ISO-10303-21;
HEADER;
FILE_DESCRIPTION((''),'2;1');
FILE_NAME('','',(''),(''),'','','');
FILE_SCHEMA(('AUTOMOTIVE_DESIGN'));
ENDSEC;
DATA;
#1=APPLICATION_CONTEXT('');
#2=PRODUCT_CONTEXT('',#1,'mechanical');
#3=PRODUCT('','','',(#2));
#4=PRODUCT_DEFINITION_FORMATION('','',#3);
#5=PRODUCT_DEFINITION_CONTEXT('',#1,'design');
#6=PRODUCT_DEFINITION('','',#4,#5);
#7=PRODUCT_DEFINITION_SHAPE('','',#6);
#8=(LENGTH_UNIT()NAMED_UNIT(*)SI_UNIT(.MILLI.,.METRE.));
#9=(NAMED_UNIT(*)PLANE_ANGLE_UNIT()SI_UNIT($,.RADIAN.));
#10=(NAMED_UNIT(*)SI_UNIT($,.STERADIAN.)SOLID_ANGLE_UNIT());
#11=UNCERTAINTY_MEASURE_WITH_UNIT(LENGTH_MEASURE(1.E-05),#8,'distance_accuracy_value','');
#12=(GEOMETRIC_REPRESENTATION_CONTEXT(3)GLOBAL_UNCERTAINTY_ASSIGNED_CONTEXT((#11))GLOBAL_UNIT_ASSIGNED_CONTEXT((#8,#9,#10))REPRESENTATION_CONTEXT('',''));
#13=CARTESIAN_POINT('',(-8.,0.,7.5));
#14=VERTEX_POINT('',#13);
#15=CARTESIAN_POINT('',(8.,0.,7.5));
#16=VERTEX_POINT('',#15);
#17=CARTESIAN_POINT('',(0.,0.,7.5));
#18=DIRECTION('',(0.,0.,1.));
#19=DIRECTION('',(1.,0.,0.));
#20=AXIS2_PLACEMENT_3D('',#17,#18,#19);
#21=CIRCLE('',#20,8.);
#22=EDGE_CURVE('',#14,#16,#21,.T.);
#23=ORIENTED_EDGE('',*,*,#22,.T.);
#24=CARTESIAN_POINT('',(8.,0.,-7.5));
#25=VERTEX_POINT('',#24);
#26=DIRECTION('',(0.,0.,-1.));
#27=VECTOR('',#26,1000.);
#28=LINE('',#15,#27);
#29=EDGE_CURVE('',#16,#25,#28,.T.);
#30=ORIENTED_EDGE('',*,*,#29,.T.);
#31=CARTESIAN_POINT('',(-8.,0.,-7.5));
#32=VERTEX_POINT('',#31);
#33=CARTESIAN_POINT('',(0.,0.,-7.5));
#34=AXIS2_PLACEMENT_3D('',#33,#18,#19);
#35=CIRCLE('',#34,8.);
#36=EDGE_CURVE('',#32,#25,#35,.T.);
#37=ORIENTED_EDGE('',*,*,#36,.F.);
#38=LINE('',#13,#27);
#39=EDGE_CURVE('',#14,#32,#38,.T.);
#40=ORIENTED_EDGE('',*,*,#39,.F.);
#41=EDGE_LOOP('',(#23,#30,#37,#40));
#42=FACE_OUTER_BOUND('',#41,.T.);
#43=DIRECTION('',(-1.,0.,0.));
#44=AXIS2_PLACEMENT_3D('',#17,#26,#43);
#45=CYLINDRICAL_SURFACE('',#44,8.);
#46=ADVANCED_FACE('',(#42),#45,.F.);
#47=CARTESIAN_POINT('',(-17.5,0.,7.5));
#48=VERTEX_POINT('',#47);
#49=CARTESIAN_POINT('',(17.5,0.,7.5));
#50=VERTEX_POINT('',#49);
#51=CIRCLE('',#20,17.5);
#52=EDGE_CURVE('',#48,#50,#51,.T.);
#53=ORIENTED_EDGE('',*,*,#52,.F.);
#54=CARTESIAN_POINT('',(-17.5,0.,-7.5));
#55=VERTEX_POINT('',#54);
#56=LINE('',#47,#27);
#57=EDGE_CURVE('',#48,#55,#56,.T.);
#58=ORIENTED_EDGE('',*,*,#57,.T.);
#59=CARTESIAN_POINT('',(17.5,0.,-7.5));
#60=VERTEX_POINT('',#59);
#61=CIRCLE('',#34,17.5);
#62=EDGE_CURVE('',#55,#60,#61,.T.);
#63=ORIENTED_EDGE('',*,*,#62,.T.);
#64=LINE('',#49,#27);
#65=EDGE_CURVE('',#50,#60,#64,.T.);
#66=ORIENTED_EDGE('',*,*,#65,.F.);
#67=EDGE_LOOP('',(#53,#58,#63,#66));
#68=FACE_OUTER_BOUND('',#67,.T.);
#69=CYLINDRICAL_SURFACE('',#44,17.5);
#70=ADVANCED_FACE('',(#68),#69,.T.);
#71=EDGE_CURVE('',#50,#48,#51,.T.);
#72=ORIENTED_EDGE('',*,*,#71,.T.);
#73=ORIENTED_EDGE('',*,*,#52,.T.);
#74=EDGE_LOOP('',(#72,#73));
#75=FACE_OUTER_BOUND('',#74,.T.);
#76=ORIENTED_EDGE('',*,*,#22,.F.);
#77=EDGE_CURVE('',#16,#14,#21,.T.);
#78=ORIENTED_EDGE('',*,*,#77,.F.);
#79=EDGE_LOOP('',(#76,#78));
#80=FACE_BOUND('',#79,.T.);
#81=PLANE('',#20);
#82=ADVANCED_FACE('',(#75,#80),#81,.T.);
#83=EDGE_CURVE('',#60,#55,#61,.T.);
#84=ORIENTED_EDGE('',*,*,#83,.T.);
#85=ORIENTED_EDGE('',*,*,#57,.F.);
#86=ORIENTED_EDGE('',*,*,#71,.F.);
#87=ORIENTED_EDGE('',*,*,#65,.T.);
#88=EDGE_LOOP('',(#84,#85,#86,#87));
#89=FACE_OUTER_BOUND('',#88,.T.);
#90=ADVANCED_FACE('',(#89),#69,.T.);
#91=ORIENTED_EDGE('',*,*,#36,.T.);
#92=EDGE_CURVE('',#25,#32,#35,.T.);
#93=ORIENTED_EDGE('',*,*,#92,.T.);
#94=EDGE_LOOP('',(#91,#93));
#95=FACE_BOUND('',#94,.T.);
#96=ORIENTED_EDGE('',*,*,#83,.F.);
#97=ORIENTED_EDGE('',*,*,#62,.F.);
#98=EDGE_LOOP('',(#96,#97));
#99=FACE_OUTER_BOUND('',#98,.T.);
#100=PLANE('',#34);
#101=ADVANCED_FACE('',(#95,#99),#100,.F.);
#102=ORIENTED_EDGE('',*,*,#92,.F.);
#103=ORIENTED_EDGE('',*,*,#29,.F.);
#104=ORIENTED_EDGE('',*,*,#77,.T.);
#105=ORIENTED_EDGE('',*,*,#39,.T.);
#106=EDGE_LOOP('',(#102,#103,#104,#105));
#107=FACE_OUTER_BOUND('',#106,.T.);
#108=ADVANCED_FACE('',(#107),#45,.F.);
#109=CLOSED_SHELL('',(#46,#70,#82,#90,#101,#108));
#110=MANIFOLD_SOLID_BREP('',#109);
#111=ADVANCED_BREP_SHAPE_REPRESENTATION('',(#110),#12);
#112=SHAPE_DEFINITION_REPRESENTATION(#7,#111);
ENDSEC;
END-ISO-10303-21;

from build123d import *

# Parameters (mm, degrees)
SKETCH_1_R      = 17.5
SKETCH_1_R_2    = 8
EXTRUDE_1_DEPTH = 7.5


with BuildPart() as part:
    # 草图1 → 凸台-拉伸1 (new, symmetric)
    with BuildSketch(Plane.XY):
        Circle(SKETCH_1_R)
        Circle(SKETCH_1_R_2, mode=Mode.SUBTRACT)
    extrude(amount=EXTRUDE_1_DEPTH, both=True)


solid = part.part
